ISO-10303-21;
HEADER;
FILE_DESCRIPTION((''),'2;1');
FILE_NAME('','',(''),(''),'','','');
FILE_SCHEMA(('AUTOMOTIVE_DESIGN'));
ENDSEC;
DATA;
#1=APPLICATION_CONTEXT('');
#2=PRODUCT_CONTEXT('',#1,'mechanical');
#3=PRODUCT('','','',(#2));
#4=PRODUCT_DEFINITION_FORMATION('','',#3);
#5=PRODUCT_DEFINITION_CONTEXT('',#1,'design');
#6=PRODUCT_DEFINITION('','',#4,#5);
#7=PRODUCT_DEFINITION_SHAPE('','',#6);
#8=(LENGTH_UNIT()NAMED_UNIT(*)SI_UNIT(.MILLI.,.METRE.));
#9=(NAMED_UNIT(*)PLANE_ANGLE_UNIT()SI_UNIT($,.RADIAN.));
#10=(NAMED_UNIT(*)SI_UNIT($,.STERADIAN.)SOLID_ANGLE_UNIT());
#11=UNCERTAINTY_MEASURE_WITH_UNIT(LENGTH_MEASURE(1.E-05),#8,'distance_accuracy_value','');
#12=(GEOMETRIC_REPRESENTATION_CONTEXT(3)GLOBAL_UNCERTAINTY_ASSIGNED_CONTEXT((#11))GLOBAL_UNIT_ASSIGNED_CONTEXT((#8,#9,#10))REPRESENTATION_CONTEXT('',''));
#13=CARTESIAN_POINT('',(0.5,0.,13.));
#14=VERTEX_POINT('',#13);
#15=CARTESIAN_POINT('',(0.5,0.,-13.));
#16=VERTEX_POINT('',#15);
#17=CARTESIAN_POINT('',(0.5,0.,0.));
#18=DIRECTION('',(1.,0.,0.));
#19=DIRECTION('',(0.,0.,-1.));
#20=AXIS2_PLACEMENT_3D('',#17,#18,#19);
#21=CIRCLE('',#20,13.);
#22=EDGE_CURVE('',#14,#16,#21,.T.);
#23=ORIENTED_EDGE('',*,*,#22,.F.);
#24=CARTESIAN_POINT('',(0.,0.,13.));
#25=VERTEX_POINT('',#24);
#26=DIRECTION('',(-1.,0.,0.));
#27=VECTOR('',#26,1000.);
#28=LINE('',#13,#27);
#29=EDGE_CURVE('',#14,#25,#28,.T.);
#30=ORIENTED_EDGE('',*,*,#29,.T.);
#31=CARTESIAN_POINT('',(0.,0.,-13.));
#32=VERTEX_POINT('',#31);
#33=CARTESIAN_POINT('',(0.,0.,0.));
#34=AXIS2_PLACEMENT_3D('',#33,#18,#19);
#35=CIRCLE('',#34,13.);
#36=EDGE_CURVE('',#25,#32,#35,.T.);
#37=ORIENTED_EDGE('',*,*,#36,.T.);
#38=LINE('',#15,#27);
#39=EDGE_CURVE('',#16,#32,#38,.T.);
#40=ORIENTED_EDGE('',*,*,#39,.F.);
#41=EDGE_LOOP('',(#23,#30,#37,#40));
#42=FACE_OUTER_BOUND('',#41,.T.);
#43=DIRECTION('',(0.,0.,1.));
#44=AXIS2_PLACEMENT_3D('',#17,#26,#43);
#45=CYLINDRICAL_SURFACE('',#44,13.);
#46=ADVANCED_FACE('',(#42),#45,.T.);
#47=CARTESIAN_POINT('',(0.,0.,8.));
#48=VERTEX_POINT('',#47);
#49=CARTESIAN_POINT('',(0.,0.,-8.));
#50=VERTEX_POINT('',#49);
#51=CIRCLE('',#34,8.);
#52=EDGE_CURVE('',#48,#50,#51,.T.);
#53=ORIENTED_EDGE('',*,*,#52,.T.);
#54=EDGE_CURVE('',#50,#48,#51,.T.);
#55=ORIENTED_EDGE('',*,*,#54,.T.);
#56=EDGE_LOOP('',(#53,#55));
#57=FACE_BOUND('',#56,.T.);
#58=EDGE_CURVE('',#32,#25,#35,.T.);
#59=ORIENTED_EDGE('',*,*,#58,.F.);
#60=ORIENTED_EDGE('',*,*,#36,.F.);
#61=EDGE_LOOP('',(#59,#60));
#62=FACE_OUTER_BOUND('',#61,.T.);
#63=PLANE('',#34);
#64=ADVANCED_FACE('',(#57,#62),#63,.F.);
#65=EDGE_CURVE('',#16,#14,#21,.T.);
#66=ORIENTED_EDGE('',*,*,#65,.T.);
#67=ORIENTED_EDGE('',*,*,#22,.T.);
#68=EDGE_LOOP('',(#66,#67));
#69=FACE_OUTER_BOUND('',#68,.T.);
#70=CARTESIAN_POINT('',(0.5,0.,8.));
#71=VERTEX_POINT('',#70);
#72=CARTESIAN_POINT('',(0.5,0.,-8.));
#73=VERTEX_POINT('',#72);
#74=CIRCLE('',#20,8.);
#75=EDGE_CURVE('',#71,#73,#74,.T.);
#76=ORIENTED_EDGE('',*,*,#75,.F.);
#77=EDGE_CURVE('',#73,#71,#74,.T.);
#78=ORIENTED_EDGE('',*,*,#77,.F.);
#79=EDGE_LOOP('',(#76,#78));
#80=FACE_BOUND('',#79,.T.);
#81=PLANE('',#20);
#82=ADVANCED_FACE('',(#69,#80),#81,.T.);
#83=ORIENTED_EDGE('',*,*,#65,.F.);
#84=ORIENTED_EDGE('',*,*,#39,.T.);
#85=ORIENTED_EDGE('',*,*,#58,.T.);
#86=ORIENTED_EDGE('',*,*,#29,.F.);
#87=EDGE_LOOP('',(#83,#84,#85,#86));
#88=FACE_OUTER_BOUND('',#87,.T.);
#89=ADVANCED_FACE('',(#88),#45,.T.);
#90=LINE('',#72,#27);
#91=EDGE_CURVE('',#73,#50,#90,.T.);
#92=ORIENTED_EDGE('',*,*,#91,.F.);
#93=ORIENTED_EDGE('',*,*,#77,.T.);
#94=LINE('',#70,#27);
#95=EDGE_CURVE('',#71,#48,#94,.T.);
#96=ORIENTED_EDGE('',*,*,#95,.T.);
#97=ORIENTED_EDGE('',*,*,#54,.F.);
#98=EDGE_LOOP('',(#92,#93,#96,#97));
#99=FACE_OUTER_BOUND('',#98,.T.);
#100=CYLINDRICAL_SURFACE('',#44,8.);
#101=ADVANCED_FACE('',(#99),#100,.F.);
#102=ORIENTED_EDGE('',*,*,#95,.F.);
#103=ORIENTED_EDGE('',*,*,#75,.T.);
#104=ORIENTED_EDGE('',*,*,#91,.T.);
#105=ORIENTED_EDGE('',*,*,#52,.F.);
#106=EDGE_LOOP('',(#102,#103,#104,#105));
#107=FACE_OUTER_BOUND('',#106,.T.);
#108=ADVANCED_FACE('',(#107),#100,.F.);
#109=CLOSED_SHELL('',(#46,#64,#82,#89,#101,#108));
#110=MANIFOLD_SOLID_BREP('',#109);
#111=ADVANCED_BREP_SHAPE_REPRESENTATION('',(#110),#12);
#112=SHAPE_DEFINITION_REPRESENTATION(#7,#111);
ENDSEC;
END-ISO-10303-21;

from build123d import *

# Parameters (mm, degrees)
SKETCH1_R           = 13
SKETCH1_R_2         = 8
BOSS_EXTRUDE1_DEPTH = 0.5


with BuildPart() as part:
    # Sketch1 → Boss-Extrude1 (new body)
    with BuildSketch(Plane(origin=(0, 0, 0), x_dir=(0, 0, -1), z_dir=(1, 0, 0))):
        Circle(SKETCH1_R)
        Circle(SKETCH1_R_2, mode=Mode.SUBTRACT)
    extrude(amount=BOSS_EXTRUDE1_DEPTH)


solid = part.part
